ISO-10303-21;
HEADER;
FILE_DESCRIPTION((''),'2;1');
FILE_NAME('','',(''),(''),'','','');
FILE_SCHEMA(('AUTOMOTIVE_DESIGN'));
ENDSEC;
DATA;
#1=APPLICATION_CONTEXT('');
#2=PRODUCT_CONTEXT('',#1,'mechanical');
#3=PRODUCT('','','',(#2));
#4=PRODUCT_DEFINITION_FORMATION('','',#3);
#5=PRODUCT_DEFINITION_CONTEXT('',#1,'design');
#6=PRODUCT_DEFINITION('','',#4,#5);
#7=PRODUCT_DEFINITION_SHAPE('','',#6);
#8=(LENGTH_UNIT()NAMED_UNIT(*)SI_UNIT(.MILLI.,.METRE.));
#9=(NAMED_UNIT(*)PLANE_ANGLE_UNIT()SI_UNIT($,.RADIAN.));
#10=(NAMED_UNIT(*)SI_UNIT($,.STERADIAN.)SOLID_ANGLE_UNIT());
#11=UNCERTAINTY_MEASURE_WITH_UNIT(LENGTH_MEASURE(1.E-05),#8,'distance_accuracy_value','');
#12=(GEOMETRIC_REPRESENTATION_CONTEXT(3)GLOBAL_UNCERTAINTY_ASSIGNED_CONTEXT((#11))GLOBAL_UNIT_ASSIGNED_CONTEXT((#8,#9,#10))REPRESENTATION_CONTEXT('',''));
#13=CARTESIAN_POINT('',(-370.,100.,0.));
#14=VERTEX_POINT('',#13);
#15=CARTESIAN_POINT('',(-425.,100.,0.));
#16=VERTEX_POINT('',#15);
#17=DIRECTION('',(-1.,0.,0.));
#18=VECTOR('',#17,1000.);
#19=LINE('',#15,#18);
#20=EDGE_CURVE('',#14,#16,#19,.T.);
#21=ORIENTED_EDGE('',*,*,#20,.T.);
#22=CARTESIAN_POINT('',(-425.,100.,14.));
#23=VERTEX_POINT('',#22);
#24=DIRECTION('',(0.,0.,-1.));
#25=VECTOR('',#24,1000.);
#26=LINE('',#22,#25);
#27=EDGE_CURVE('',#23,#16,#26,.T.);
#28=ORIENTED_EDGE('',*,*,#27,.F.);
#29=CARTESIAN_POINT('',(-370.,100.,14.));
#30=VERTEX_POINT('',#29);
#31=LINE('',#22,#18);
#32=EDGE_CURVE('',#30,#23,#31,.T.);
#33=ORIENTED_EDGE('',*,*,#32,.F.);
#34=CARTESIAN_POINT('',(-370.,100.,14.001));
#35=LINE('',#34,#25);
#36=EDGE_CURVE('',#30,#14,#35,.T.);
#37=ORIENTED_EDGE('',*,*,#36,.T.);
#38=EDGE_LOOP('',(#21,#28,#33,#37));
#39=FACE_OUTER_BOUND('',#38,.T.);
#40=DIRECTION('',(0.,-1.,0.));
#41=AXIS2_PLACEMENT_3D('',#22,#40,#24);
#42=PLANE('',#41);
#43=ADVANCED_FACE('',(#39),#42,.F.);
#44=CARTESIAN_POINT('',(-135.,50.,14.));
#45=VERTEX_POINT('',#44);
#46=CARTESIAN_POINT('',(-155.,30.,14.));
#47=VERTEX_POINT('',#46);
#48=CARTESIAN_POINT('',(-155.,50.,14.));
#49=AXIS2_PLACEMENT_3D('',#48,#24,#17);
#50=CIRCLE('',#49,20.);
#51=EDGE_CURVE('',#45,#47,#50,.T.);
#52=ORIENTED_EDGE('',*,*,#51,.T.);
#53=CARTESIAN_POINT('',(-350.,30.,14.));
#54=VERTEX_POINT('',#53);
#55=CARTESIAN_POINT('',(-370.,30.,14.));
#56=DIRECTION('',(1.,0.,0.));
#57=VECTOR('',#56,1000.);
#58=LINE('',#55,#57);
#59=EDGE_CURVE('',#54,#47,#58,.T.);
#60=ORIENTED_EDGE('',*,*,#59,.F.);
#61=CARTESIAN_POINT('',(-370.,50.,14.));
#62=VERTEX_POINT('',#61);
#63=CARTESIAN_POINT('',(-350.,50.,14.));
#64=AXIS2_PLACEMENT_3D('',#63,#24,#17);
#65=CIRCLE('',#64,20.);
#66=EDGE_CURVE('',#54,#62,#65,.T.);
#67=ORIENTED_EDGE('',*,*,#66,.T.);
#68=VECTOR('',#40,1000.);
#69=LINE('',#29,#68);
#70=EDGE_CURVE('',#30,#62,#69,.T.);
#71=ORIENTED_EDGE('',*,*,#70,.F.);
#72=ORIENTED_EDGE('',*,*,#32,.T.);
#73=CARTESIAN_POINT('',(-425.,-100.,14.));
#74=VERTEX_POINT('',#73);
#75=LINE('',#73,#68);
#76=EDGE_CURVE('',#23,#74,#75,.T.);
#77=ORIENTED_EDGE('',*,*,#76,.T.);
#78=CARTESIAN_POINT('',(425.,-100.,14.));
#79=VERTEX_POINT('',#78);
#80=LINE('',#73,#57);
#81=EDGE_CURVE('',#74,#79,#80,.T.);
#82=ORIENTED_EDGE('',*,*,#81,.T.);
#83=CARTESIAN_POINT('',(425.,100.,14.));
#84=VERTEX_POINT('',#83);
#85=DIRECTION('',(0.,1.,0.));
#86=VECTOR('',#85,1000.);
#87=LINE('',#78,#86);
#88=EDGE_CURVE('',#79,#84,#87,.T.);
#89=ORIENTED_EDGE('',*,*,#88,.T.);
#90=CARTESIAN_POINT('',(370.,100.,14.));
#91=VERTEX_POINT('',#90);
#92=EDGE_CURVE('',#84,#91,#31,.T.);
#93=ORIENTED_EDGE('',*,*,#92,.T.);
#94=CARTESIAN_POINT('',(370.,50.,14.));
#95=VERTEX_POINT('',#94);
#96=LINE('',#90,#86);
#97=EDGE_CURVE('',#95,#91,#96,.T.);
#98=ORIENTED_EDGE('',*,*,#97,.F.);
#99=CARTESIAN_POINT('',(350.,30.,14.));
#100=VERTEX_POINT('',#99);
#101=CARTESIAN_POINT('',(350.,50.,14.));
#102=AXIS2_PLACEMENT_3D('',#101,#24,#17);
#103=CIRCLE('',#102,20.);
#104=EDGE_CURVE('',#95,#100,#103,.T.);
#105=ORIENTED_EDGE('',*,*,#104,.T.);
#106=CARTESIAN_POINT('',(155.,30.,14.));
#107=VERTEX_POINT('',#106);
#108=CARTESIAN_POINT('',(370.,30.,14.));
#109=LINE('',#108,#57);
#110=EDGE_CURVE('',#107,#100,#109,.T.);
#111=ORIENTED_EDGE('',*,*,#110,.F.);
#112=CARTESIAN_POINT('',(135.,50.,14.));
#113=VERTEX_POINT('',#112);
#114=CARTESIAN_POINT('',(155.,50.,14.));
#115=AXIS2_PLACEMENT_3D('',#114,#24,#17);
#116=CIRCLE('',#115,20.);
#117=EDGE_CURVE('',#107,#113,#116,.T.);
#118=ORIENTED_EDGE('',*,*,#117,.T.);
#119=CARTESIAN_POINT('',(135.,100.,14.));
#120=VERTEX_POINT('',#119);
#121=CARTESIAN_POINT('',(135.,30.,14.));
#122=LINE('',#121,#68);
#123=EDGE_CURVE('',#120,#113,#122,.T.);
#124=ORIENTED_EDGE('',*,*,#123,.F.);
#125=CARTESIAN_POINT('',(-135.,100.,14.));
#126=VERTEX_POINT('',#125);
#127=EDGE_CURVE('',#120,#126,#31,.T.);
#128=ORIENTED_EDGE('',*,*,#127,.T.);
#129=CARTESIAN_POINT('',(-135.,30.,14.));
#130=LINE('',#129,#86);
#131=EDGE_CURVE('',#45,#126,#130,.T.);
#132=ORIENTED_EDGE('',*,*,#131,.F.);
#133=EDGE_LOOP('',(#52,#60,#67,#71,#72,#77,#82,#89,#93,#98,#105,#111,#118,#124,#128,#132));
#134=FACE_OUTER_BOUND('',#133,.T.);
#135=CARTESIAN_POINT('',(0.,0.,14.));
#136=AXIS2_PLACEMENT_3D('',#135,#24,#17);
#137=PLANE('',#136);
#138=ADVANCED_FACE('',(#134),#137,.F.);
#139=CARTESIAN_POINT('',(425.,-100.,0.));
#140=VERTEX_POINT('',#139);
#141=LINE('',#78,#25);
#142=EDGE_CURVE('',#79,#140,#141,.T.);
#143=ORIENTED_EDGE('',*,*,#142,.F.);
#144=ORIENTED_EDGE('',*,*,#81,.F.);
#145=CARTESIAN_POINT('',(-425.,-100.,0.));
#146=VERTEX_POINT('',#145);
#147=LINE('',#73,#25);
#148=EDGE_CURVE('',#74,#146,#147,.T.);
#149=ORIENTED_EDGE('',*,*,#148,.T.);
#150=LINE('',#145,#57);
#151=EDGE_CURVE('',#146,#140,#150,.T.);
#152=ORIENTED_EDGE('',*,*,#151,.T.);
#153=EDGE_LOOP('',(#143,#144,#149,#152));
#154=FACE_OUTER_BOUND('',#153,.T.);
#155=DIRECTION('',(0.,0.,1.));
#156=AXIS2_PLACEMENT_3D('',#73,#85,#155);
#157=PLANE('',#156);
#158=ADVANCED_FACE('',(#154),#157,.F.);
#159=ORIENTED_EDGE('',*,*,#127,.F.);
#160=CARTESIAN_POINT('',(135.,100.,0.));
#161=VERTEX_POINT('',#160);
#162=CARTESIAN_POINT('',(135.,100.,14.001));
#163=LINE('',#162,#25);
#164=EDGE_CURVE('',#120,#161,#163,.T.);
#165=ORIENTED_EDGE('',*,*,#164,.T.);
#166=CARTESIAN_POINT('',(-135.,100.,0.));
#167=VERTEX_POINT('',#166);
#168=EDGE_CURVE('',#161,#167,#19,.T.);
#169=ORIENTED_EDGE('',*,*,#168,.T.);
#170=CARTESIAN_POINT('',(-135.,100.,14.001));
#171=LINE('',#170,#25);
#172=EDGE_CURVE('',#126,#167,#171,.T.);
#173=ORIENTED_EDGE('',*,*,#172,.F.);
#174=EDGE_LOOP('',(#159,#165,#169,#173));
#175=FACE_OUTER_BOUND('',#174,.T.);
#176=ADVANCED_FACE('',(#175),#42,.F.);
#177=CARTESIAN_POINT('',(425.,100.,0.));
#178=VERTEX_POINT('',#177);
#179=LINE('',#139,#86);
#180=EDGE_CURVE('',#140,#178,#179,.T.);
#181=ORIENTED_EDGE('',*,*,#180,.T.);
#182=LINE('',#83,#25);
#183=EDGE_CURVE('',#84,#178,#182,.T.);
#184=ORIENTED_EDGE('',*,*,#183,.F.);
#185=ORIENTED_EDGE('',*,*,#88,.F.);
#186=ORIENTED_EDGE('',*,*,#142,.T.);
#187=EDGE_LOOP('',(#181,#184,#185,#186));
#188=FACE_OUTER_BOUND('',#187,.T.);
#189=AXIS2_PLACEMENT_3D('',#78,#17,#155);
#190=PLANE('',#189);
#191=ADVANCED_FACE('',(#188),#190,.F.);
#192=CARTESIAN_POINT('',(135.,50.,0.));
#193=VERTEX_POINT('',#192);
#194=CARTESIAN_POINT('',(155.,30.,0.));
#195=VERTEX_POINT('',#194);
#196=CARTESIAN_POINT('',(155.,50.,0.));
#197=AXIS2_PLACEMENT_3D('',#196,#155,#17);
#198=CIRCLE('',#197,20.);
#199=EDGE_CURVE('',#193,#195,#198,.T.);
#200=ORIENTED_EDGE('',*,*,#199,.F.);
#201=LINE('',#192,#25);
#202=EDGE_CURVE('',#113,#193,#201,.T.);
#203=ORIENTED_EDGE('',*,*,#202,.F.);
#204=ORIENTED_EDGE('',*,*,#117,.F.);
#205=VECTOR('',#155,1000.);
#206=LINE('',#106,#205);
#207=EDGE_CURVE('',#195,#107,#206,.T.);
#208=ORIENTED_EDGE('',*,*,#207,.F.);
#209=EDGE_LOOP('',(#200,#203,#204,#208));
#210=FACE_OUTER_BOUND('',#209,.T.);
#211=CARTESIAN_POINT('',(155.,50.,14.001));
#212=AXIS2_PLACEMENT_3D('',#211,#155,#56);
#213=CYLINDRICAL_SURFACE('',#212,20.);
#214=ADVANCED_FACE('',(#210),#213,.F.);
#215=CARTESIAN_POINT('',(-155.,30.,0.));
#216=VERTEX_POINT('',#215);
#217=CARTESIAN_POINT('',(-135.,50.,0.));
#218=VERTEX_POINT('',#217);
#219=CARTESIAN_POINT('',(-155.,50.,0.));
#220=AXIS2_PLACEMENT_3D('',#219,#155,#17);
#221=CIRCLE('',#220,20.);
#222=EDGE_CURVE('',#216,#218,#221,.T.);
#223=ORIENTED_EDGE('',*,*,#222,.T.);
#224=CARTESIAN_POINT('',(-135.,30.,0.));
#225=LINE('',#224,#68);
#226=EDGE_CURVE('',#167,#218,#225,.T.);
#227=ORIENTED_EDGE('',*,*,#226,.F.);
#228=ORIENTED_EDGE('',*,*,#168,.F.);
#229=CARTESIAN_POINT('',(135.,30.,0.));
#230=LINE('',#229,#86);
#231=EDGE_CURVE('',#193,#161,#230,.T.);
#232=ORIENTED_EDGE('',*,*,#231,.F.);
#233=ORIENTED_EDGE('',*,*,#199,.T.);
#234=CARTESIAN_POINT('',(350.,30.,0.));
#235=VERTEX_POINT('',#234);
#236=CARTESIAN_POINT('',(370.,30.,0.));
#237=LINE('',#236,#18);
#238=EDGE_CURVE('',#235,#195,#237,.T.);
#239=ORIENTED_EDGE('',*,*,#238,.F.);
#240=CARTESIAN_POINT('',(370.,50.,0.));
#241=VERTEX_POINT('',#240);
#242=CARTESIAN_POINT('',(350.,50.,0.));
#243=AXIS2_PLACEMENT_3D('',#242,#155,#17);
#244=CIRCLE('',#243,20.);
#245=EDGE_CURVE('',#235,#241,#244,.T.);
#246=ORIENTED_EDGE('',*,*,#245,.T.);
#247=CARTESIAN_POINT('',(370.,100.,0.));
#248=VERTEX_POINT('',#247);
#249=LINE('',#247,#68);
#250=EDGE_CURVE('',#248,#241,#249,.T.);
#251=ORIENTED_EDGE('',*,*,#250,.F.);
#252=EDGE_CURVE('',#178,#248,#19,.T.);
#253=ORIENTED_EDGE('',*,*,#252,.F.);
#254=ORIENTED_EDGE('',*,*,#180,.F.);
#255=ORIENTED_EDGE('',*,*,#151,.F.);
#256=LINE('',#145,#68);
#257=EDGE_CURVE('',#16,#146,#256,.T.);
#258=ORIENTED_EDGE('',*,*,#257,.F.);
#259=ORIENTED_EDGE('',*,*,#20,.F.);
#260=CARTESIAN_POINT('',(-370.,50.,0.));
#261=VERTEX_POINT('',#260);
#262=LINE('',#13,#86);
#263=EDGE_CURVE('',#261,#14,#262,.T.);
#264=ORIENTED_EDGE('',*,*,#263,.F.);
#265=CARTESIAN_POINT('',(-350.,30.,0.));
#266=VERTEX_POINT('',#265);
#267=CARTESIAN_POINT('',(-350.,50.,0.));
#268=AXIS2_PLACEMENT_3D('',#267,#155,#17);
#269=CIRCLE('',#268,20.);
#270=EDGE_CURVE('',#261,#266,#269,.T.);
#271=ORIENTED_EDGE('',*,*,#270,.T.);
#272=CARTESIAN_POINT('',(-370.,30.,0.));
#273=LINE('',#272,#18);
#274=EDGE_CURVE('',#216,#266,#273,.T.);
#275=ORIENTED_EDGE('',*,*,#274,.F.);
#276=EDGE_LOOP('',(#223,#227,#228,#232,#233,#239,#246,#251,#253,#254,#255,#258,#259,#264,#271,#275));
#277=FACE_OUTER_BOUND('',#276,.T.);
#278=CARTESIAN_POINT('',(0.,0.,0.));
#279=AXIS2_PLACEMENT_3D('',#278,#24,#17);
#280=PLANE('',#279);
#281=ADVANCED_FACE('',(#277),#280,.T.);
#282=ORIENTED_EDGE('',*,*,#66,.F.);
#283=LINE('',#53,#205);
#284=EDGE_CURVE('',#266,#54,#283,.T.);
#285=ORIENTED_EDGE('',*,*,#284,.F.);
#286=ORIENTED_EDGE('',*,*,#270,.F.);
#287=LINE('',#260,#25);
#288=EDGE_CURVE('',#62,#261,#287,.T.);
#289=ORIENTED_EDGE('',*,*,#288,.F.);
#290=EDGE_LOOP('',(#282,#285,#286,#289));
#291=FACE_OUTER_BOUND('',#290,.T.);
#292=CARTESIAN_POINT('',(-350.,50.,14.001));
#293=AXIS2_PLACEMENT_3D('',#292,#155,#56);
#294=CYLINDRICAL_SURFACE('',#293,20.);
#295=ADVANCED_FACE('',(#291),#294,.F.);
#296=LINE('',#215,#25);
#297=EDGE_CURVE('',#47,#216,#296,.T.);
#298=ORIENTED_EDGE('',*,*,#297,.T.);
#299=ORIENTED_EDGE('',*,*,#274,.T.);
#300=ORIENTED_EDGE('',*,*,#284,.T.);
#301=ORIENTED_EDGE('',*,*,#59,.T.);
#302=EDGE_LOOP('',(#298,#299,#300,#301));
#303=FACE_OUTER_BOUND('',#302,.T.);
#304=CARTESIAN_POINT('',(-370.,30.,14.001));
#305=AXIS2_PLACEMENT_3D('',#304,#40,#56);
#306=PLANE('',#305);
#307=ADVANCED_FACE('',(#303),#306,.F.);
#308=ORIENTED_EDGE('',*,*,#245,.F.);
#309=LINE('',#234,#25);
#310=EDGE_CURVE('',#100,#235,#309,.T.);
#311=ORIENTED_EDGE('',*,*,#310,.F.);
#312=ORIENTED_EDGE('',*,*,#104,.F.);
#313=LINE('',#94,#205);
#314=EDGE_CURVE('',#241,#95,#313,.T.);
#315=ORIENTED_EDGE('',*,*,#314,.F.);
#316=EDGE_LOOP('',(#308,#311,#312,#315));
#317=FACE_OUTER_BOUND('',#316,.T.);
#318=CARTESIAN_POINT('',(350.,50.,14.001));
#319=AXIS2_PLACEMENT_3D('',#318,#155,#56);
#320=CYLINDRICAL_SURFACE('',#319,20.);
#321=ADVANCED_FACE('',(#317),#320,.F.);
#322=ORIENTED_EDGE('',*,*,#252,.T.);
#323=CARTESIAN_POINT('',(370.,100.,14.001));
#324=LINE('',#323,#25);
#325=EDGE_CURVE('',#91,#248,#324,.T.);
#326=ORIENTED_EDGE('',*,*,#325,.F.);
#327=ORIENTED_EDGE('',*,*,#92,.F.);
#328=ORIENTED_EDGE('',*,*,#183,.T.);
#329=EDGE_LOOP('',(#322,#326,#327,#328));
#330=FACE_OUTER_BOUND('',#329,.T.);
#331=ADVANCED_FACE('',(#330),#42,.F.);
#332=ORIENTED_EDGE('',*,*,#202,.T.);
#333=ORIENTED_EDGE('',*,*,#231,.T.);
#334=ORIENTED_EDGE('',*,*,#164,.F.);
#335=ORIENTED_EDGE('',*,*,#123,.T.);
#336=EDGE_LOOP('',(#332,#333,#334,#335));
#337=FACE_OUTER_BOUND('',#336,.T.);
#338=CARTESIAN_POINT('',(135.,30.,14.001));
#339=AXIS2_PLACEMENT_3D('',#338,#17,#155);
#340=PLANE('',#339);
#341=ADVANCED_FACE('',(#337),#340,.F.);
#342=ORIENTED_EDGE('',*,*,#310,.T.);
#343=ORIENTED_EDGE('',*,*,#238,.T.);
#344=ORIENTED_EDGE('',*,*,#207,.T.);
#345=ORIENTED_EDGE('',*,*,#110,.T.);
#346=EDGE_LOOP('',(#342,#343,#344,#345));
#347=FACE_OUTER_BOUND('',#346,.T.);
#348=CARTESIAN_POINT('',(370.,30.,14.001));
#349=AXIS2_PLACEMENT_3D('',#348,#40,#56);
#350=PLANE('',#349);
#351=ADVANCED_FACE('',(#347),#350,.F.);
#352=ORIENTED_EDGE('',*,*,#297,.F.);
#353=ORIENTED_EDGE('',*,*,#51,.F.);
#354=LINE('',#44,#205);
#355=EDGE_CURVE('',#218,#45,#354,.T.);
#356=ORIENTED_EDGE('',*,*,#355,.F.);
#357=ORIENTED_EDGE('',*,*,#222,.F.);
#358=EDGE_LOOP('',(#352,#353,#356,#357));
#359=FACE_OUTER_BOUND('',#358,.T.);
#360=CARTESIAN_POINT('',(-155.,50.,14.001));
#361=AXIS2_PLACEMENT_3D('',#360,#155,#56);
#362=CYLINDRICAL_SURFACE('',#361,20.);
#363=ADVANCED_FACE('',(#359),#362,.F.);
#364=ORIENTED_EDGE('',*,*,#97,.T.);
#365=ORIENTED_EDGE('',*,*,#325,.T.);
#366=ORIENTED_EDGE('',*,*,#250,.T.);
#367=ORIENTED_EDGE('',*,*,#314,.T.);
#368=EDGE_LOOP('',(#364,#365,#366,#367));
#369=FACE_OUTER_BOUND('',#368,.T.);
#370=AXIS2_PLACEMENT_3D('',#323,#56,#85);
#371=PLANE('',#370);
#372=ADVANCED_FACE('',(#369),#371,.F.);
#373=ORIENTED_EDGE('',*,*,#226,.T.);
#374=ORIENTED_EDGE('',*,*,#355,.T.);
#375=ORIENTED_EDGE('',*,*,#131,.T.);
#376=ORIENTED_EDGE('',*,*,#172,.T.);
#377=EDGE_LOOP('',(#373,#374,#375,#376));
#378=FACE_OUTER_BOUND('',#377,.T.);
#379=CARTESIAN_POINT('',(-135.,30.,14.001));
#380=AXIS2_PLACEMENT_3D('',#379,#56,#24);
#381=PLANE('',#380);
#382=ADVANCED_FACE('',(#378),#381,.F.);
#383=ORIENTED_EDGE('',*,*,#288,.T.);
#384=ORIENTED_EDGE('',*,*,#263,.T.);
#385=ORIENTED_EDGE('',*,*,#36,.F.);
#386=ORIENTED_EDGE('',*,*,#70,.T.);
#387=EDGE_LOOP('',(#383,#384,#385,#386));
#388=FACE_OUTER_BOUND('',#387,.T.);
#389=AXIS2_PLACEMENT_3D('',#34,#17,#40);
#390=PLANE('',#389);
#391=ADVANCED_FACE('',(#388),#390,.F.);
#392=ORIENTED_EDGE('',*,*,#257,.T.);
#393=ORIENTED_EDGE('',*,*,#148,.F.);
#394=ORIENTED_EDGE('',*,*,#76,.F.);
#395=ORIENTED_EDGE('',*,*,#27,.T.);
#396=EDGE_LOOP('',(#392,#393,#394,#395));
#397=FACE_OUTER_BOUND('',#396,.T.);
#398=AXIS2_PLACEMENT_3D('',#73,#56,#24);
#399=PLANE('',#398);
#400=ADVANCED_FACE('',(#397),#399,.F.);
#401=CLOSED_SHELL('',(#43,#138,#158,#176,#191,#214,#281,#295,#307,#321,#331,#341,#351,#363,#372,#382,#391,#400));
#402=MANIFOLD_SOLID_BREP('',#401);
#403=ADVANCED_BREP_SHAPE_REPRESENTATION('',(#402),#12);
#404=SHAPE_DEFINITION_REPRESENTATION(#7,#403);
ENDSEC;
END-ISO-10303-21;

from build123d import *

# Parameters (mm, degrees)
SKETCH_1_W          = 850
SKETCH_1_H          = 200
EXTRUDE_1_DEPTH     = 14
CUT_EXTRUDE_1_REACH = 438.831
SKETCH_2_W          = 235
SKETCH_2_H          = 70
FILLET_1_R          = 20


with BuildPart() as part:
    # 草图1 → 凸台-拉伸1 (new body)
    with BuildSketch(Plane.XY):
        Rectangle(SKETCH_1_W, SKETCH_1_H)
    extrude(amount=EXTRUDE_1_DEPTH)

    # 草图2 → 切除-拉伸1 (cut, up to next)
    with BuildSketch(Plane(origin=(0, 0, 0), x_dir=(-1, 0, 0), z_dir=(0, 0, -1)), mode=Mode.PRIVATE) as cut_extrude_1_sk1:
        with Locations((252.5, 65)):
            Rectangle(SKETCH_2_W, SKETCH_2_H)
    cut_extrude_1_tool1 = extrude(cut_extrude_1_sk1.sketch, amount=-CUT_EXTRUDE_1_REACH, mode=Mode.PRIVATE) & part.part
    # 草图2 → 切除-拉伸1 (cut, up to next)
    with BuildSketch(Plane(origin=(0, 0, 0), x_dir=(-1, 0, 0), z_dir=(0, 0, -1)), mode=Mode.PRIVATE) as cut_extrude_1_sk2:
        with Locations((-252.5, 65)):
            Rectangle(SKETCH_2_W, SKETCH_2_H)
    cut_extrude_1_tool2 = extrude(cut_extrude_1_sk2.sketch, amount=-CUT_EXTRUDE_1_REACH, mode=Mode.PRIVATE) & part.part
    add(cut_extrude_1_tool1.solids().sort_by_distance((-252.5, 65, 0))[0], mode=Mode.SUBTRACT)
    add(cut_extrude_1_tool2.solids().sort_by_distance((252.5, 65, 0))[0], mode=Mode.SUBTRACT)

    # 圆角1
    fillet_1_edges = [part.edges().sort_by_distance(p)[0] for p in [
        (-370, 30, 7),
        (-135, 30, 7),
        (135, 30, 7),
        (370, 30, 7),
    ]]
    fillet(fillet_1_edges, radius=FILLET_1_R)


solid = part.part
